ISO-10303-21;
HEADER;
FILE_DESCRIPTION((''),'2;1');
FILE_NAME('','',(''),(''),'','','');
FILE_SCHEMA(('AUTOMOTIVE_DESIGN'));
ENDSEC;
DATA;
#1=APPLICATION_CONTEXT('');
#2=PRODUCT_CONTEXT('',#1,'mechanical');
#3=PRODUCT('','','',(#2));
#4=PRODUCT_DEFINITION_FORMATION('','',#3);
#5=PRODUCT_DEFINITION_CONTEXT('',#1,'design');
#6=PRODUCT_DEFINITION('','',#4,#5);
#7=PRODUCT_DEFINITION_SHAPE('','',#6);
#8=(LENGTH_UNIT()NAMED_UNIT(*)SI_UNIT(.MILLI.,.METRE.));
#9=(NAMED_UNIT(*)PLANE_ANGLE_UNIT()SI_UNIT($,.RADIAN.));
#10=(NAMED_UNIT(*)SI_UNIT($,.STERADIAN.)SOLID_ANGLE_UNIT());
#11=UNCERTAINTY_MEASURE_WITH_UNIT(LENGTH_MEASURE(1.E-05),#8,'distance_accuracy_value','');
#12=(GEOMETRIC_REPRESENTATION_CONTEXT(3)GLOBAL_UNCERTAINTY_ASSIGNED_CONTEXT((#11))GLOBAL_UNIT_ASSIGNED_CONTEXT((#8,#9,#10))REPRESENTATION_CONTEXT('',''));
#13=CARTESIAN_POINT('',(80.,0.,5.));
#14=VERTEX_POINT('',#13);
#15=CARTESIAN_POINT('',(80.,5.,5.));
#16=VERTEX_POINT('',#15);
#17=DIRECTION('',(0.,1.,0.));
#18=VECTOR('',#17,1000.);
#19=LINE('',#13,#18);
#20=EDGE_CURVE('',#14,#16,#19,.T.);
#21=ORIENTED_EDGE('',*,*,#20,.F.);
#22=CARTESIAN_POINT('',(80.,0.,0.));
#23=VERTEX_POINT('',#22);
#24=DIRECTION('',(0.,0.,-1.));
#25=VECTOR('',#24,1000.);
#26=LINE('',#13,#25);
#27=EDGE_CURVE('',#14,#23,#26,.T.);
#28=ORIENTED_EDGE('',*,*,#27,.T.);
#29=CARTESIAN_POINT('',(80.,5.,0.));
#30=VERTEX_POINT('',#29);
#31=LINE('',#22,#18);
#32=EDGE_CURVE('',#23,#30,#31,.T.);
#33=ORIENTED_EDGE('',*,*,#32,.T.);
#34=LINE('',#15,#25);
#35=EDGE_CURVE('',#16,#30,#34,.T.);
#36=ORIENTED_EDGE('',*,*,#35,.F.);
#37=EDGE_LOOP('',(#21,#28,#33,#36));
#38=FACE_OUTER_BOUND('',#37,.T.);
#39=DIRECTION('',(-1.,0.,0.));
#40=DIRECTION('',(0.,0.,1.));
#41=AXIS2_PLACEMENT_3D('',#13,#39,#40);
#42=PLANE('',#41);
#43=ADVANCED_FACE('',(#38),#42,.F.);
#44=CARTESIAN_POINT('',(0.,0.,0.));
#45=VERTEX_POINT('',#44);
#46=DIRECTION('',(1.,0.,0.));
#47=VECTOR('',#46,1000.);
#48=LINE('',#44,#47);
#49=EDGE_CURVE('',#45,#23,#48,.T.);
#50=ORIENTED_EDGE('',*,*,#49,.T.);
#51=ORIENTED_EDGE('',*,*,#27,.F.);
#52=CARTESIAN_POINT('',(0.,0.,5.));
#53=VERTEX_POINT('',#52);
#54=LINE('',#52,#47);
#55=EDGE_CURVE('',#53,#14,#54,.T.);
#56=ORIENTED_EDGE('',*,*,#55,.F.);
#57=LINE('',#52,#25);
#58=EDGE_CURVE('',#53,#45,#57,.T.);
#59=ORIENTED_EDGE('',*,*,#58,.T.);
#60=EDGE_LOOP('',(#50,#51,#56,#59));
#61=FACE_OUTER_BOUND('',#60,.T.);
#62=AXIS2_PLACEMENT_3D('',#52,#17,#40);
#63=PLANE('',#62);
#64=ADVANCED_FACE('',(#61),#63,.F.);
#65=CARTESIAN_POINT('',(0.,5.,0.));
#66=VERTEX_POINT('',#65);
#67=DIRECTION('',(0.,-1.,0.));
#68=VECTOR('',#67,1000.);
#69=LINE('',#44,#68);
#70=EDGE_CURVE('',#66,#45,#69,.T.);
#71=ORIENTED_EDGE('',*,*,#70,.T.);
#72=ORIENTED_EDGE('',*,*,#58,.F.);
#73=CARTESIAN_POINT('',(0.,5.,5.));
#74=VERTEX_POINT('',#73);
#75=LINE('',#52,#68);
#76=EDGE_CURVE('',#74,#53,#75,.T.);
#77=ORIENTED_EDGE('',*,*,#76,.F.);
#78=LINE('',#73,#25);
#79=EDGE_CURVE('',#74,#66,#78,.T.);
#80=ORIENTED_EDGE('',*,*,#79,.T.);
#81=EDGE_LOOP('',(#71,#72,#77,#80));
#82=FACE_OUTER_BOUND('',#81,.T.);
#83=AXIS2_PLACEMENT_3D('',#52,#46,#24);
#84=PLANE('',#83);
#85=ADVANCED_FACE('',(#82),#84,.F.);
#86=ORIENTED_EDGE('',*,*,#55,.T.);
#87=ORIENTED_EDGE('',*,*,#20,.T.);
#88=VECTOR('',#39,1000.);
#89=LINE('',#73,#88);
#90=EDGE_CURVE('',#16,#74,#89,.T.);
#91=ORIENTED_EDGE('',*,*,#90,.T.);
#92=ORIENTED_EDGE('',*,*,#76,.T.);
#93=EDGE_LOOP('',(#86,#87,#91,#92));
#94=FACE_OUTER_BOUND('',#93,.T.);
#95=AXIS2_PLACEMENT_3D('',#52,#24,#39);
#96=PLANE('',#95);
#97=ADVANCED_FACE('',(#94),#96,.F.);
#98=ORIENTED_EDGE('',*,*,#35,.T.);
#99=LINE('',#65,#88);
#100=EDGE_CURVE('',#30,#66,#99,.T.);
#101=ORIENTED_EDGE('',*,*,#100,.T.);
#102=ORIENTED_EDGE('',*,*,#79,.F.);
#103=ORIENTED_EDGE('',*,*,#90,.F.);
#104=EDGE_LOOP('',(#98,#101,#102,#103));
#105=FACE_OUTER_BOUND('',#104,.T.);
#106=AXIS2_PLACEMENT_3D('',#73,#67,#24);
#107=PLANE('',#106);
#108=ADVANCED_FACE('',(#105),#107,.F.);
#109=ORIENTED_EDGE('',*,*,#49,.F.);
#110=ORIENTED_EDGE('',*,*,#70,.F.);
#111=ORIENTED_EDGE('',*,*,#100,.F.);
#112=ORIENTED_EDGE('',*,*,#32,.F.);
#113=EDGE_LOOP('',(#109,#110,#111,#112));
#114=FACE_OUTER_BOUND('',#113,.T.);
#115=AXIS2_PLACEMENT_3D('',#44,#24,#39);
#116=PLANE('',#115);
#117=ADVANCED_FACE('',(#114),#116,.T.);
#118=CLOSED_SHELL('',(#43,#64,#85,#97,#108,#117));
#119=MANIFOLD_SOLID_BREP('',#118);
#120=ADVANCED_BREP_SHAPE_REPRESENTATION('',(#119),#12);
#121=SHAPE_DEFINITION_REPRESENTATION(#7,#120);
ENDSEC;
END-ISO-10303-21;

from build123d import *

# Parameters (mm, degrees)
SKETCH_1_W      = 80
SKETCH_1_H      = 5
EXTRUDE_1_DEPTH = 5


with BuildPart() as part:
    # 草图1 → 凸台-拉伸1 (new body)
    with BuildSketch(Plane.XY):
        with Locations((40, 2.5)):
            Rectangle(SKETCH_1_W, SKETCH_1_H)
    extrude(amount=EXTRUDE_1_DEPTH)


solid = part.part
